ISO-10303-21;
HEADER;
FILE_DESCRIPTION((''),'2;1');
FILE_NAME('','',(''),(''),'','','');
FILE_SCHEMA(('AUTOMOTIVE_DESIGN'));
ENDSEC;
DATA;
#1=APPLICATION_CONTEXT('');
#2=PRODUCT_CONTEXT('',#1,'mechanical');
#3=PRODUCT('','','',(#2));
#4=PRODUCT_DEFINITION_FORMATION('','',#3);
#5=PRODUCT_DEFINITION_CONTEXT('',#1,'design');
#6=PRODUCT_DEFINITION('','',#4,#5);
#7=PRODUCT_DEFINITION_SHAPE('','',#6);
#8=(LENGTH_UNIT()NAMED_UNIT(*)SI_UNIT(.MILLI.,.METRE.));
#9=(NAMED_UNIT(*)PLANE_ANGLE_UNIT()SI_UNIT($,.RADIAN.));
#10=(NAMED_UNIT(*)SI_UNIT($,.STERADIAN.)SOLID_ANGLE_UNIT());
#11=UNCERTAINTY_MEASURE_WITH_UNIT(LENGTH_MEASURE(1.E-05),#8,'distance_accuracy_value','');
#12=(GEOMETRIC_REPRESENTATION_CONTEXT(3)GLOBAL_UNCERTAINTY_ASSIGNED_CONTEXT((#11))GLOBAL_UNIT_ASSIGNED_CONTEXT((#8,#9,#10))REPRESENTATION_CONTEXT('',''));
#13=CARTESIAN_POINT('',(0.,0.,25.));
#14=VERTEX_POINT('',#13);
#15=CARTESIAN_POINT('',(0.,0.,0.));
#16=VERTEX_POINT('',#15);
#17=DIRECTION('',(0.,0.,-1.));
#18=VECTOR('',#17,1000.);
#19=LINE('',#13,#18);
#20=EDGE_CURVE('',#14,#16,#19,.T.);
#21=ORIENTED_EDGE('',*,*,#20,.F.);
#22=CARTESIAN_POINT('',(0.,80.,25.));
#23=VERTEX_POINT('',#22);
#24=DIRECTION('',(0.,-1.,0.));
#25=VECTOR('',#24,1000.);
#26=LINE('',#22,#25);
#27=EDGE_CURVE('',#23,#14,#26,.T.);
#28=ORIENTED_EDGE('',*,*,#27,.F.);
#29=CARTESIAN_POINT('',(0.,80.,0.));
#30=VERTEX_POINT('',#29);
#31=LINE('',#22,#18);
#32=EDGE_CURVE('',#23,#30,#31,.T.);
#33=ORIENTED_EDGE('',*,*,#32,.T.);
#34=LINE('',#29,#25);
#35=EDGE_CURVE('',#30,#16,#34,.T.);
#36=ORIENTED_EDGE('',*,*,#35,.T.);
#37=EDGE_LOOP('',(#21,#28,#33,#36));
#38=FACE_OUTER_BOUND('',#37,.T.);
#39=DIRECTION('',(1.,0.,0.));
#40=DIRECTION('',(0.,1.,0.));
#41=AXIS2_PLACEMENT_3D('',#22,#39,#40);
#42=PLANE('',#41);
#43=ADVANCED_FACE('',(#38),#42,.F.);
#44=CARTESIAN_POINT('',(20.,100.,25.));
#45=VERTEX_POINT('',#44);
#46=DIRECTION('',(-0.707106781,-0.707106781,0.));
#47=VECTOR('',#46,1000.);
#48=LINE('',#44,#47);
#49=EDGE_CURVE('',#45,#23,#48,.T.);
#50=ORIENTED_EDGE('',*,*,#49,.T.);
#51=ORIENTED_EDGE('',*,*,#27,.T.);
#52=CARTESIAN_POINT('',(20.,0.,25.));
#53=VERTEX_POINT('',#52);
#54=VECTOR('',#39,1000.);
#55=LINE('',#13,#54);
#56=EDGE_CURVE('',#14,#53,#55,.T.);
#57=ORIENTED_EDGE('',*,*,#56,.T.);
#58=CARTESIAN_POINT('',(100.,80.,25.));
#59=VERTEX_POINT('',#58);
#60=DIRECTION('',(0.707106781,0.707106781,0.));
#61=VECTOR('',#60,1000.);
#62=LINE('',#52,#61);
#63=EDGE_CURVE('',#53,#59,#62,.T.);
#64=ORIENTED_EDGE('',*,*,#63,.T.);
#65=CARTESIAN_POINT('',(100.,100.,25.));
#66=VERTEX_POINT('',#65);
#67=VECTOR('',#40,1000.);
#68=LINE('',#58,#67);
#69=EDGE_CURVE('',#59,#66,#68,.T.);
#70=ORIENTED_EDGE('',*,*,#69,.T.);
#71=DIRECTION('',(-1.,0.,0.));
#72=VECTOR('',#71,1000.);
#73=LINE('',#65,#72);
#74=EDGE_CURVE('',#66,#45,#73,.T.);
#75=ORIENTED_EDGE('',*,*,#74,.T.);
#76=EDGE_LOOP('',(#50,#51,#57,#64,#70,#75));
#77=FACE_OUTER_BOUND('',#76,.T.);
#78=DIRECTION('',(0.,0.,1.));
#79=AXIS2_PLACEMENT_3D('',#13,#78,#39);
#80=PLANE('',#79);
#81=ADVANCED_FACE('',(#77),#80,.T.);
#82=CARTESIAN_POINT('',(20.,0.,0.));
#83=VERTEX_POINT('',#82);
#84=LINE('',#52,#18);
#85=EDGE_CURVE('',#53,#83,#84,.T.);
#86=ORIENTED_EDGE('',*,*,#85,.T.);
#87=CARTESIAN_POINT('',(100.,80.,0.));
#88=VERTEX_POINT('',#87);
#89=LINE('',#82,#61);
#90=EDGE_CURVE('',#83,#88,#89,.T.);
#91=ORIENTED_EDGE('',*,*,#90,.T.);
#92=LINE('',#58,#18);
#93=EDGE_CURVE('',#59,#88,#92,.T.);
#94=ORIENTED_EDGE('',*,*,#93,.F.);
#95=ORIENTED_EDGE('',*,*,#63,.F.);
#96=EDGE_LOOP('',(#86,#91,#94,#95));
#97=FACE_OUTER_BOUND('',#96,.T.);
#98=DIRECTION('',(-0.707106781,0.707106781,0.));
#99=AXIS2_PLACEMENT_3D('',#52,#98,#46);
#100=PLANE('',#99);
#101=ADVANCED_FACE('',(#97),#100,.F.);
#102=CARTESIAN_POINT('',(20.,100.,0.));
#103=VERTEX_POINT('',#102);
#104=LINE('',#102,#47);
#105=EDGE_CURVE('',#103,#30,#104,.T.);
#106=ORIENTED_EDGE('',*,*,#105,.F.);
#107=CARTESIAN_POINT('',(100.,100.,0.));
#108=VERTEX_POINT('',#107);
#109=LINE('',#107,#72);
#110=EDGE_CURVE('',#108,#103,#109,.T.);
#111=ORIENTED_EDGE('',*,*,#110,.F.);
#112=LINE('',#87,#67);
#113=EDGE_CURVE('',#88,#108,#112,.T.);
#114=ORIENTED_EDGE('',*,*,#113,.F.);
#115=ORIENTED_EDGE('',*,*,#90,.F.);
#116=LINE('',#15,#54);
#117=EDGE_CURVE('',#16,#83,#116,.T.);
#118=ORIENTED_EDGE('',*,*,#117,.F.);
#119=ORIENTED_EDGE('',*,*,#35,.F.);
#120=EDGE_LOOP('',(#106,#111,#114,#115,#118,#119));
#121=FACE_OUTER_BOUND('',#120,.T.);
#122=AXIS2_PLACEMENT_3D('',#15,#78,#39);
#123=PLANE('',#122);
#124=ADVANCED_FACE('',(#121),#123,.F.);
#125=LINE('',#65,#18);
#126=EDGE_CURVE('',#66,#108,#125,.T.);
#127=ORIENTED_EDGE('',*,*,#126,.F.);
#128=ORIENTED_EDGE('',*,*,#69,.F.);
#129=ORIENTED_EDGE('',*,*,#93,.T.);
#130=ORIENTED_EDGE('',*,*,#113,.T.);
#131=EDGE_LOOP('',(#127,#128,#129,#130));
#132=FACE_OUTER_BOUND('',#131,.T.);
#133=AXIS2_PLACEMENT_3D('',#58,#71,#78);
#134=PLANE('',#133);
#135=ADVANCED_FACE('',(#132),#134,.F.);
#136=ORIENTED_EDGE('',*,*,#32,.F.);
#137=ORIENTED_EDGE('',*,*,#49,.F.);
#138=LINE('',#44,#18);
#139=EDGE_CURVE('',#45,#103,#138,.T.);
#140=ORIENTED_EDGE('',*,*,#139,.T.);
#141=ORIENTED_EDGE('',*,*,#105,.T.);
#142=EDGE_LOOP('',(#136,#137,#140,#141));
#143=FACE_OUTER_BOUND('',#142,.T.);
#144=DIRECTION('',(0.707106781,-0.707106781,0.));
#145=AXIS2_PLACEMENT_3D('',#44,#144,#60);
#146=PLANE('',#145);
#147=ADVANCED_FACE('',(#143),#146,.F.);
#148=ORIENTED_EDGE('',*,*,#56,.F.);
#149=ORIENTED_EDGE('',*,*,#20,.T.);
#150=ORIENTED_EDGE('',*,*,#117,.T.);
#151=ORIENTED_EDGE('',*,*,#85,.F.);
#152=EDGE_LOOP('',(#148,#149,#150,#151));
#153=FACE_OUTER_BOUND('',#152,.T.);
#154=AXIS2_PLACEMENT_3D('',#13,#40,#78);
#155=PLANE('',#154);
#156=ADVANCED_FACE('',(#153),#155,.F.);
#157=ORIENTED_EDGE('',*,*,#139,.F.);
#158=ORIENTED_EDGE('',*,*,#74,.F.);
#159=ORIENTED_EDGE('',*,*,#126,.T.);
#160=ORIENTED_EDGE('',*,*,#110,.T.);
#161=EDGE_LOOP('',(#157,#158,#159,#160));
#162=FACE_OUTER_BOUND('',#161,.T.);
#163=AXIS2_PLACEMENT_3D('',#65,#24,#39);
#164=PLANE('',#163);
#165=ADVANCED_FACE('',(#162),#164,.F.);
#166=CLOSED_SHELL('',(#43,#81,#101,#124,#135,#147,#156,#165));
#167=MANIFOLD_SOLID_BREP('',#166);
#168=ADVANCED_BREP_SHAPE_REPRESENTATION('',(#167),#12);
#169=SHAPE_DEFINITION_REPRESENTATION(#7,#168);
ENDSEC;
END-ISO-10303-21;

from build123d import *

# Parameters (mm, degrees)
BOSS_EXTRUDE1_DEPTH = 25


with BuildPart() as part:
    # Sketch1 → Boss-Extrude1 (new body)
    with BuildSketch(Plane.XY):
        Polygon((0, 0), (20, 0), (100, 80), (100, 100), (20, 100), (0, 80), align=None)
    extrude(amount=BOSS_EXTRUDE1_DEPTH)


solid = part.part
